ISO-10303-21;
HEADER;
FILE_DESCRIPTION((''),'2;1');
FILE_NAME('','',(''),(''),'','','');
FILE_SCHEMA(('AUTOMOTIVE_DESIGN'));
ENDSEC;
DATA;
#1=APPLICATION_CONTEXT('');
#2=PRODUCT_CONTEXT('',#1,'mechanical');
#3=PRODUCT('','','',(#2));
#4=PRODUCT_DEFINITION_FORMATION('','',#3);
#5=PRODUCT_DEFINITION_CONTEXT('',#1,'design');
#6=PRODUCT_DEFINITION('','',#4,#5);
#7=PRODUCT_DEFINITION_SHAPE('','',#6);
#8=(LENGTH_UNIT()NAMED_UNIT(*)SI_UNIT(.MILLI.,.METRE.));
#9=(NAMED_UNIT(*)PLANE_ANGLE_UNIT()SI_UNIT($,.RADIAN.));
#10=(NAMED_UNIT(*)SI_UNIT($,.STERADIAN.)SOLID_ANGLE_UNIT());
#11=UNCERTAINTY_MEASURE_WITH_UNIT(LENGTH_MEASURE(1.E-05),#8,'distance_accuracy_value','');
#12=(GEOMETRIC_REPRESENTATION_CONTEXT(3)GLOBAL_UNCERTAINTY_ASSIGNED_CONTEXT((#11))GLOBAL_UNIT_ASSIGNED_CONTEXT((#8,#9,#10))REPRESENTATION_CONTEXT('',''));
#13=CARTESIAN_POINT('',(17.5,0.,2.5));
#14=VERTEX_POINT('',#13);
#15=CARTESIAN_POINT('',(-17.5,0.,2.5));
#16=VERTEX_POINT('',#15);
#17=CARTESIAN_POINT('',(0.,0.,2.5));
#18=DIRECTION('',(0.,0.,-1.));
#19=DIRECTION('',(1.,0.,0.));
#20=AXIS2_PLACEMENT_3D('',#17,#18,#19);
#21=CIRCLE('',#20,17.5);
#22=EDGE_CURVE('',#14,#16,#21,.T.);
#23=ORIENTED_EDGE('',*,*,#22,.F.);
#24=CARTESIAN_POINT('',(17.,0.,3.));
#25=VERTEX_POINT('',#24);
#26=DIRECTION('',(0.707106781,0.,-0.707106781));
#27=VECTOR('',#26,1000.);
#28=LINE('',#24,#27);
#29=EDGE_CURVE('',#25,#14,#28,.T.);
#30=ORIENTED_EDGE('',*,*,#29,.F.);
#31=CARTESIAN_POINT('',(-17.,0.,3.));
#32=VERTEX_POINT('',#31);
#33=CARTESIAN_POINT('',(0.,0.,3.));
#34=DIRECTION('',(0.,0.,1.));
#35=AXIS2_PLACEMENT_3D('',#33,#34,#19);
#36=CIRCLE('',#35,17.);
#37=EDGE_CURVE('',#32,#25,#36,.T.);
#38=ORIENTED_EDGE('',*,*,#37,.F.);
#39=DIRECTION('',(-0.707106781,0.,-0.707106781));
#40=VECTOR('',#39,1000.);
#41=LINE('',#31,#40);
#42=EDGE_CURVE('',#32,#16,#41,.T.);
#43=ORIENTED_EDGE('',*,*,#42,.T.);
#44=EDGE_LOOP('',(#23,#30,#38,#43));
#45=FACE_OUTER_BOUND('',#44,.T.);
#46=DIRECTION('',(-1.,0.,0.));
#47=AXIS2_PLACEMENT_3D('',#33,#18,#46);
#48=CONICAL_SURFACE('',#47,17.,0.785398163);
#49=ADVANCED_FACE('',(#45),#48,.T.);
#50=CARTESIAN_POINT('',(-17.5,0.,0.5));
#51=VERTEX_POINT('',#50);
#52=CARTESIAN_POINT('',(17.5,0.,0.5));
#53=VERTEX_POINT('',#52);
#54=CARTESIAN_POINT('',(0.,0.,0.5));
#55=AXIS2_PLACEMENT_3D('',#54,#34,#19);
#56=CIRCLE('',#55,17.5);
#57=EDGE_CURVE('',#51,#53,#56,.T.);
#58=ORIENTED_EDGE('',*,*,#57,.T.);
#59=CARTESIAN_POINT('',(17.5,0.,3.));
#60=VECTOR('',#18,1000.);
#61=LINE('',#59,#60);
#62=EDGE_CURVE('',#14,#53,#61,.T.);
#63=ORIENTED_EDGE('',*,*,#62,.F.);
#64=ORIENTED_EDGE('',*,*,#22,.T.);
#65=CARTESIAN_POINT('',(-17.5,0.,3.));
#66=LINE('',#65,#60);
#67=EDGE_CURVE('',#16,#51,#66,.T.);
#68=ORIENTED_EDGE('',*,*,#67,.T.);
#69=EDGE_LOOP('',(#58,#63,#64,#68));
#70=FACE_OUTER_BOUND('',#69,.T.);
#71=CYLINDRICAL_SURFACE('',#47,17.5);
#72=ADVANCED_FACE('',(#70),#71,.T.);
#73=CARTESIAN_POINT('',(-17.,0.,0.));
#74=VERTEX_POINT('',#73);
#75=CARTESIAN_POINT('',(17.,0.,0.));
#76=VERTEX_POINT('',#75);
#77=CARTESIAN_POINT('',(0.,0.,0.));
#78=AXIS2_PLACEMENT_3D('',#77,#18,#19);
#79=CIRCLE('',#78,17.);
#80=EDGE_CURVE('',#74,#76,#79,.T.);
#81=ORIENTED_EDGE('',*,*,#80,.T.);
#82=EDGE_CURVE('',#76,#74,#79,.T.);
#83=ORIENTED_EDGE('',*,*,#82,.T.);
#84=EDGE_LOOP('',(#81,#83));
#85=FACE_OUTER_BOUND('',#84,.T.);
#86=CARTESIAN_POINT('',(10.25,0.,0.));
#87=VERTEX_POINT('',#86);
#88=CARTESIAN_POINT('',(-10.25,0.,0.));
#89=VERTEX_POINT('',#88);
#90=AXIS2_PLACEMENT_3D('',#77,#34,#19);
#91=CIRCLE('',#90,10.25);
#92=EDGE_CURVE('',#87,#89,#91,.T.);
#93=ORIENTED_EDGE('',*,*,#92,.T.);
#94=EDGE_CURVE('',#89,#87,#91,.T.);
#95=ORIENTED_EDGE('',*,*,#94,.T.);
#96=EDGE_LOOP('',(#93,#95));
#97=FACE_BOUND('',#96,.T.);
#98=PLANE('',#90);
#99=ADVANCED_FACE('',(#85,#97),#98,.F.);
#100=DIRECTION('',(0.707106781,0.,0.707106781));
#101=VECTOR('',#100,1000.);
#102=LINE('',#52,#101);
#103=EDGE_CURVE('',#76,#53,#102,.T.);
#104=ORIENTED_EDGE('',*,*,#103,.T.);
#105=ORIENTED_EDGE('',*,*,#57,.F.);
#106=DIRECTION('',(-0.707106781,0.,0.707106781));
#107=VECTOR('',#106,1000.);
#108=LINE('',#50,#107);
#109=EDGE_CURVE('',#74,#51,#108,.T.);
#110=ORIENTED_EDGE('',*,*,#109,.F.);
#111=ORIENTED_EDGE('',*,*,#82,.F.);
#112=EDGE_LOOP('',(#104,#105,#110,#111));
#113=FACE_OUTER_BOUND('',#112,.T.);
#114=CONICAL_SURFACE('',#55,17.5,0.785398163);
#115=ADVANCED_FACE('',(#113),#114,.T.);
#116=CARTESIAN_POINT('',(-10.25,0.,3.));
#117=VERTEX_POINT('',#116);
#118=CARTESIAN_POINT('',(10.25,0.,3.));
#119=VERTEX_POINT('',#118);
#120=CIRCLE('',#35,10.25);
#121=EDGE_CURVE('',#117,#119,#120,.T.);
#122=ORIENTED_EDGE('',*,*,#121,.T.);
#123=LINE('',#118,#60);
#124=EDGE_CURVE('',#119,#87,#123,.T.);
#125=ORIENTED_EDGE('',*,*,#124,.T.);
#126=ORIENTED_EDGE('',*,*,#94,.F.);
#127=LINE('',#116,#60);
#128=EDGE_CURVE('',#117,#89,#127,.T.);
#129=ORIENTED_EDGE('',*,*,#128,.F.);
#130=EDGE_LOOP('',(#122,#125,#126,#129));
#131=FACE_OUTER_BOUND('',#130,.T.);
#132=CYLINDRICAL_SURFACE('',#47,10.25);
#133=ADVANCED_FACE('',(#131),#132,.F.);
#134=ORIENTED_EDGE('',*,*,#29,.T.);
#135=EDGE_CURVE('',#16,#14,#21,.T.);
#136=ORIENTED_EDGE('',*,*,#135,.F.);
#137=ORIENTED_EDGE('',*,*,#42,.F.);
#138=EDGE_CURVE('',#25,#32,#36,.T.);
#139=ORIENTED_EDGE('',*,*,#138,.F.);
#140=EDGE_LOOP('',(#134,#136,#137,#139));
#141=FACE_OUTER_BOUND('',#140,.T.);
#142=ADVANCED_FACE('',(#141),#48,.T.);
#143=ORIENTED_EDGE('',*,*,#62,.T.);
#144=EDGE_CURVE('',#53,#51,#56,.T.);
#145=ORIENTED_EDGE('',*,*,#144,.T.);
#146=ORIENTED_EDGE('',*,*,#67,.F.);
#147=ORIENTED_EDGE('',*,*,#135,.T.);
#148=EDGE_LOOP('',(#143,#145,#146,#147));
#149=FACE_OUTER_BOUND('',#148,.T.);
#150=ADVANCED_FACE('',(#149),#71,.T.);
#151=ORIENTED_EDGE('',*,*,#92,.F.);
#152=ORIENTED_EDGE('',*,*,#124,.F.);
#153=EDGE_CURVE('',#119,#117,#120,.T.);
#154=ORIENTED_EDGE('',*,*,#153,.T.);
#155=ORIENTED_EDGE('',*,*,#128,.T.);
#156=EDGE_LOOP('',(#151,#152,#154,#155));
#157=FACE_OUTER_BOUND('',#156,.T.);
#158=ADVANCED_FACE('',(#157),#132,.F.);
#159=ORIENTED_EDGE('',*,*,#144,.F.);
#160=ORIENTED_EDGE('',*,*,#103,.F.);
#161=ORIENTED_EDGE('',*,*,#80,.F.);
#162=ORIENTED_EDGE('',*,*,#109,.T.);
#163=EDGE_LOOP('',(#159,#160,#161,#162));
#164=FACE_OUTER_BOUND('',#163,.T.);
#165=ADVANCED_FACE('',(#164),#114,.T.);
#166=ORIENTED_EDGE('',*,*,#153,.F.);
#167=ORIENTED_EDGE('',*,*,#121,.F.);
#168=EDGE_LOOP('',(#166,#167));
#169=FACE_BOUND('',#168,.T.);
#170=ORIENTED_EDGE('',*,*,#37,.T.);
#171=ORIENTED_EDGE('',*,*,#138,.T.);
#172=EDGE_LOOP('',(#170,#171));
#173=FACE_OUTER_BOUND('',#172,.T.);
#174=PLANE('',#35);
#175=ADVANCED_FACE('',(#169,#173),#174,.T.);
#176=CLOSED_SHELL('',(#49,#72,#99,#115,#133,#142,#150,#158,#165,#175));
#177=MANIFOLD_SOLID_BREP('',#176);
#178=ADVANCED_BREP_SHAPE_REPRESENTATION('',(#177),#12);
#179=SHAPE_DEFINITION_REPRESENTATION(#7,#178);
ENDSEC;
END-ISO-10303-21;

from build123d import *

# Parameters (mm, degrees)
SKETCH_1_R      = 17.5
SKETCH_1_R_2    = 10.25
EXTRUDE_1_DEPTH = 3
CHAMFER_1_SIZE  = 0.5


with BuildPart() as part:
    # 草图1 → 凸台-拉伸1 (new body)
    with BuildSketch(Plane.XY):
        Circle(SKETCH_1_R)
        Circle(SKETCH_1_R_2, mode=Mode.SUBTRACT)
    extrude(amount=EXTRUDE_1_DEPTH)

    # 倒角1
    chamfer_1_edges = [part.edges().sort_by_distance(p)[0] for p in [
        (-17.5, 0, 0),
        (-17.5, 0, 3),
    ]]
    chamfer(chamfer_1_edges, length=CHAMFER_1_SIZE)


solid = part.part
